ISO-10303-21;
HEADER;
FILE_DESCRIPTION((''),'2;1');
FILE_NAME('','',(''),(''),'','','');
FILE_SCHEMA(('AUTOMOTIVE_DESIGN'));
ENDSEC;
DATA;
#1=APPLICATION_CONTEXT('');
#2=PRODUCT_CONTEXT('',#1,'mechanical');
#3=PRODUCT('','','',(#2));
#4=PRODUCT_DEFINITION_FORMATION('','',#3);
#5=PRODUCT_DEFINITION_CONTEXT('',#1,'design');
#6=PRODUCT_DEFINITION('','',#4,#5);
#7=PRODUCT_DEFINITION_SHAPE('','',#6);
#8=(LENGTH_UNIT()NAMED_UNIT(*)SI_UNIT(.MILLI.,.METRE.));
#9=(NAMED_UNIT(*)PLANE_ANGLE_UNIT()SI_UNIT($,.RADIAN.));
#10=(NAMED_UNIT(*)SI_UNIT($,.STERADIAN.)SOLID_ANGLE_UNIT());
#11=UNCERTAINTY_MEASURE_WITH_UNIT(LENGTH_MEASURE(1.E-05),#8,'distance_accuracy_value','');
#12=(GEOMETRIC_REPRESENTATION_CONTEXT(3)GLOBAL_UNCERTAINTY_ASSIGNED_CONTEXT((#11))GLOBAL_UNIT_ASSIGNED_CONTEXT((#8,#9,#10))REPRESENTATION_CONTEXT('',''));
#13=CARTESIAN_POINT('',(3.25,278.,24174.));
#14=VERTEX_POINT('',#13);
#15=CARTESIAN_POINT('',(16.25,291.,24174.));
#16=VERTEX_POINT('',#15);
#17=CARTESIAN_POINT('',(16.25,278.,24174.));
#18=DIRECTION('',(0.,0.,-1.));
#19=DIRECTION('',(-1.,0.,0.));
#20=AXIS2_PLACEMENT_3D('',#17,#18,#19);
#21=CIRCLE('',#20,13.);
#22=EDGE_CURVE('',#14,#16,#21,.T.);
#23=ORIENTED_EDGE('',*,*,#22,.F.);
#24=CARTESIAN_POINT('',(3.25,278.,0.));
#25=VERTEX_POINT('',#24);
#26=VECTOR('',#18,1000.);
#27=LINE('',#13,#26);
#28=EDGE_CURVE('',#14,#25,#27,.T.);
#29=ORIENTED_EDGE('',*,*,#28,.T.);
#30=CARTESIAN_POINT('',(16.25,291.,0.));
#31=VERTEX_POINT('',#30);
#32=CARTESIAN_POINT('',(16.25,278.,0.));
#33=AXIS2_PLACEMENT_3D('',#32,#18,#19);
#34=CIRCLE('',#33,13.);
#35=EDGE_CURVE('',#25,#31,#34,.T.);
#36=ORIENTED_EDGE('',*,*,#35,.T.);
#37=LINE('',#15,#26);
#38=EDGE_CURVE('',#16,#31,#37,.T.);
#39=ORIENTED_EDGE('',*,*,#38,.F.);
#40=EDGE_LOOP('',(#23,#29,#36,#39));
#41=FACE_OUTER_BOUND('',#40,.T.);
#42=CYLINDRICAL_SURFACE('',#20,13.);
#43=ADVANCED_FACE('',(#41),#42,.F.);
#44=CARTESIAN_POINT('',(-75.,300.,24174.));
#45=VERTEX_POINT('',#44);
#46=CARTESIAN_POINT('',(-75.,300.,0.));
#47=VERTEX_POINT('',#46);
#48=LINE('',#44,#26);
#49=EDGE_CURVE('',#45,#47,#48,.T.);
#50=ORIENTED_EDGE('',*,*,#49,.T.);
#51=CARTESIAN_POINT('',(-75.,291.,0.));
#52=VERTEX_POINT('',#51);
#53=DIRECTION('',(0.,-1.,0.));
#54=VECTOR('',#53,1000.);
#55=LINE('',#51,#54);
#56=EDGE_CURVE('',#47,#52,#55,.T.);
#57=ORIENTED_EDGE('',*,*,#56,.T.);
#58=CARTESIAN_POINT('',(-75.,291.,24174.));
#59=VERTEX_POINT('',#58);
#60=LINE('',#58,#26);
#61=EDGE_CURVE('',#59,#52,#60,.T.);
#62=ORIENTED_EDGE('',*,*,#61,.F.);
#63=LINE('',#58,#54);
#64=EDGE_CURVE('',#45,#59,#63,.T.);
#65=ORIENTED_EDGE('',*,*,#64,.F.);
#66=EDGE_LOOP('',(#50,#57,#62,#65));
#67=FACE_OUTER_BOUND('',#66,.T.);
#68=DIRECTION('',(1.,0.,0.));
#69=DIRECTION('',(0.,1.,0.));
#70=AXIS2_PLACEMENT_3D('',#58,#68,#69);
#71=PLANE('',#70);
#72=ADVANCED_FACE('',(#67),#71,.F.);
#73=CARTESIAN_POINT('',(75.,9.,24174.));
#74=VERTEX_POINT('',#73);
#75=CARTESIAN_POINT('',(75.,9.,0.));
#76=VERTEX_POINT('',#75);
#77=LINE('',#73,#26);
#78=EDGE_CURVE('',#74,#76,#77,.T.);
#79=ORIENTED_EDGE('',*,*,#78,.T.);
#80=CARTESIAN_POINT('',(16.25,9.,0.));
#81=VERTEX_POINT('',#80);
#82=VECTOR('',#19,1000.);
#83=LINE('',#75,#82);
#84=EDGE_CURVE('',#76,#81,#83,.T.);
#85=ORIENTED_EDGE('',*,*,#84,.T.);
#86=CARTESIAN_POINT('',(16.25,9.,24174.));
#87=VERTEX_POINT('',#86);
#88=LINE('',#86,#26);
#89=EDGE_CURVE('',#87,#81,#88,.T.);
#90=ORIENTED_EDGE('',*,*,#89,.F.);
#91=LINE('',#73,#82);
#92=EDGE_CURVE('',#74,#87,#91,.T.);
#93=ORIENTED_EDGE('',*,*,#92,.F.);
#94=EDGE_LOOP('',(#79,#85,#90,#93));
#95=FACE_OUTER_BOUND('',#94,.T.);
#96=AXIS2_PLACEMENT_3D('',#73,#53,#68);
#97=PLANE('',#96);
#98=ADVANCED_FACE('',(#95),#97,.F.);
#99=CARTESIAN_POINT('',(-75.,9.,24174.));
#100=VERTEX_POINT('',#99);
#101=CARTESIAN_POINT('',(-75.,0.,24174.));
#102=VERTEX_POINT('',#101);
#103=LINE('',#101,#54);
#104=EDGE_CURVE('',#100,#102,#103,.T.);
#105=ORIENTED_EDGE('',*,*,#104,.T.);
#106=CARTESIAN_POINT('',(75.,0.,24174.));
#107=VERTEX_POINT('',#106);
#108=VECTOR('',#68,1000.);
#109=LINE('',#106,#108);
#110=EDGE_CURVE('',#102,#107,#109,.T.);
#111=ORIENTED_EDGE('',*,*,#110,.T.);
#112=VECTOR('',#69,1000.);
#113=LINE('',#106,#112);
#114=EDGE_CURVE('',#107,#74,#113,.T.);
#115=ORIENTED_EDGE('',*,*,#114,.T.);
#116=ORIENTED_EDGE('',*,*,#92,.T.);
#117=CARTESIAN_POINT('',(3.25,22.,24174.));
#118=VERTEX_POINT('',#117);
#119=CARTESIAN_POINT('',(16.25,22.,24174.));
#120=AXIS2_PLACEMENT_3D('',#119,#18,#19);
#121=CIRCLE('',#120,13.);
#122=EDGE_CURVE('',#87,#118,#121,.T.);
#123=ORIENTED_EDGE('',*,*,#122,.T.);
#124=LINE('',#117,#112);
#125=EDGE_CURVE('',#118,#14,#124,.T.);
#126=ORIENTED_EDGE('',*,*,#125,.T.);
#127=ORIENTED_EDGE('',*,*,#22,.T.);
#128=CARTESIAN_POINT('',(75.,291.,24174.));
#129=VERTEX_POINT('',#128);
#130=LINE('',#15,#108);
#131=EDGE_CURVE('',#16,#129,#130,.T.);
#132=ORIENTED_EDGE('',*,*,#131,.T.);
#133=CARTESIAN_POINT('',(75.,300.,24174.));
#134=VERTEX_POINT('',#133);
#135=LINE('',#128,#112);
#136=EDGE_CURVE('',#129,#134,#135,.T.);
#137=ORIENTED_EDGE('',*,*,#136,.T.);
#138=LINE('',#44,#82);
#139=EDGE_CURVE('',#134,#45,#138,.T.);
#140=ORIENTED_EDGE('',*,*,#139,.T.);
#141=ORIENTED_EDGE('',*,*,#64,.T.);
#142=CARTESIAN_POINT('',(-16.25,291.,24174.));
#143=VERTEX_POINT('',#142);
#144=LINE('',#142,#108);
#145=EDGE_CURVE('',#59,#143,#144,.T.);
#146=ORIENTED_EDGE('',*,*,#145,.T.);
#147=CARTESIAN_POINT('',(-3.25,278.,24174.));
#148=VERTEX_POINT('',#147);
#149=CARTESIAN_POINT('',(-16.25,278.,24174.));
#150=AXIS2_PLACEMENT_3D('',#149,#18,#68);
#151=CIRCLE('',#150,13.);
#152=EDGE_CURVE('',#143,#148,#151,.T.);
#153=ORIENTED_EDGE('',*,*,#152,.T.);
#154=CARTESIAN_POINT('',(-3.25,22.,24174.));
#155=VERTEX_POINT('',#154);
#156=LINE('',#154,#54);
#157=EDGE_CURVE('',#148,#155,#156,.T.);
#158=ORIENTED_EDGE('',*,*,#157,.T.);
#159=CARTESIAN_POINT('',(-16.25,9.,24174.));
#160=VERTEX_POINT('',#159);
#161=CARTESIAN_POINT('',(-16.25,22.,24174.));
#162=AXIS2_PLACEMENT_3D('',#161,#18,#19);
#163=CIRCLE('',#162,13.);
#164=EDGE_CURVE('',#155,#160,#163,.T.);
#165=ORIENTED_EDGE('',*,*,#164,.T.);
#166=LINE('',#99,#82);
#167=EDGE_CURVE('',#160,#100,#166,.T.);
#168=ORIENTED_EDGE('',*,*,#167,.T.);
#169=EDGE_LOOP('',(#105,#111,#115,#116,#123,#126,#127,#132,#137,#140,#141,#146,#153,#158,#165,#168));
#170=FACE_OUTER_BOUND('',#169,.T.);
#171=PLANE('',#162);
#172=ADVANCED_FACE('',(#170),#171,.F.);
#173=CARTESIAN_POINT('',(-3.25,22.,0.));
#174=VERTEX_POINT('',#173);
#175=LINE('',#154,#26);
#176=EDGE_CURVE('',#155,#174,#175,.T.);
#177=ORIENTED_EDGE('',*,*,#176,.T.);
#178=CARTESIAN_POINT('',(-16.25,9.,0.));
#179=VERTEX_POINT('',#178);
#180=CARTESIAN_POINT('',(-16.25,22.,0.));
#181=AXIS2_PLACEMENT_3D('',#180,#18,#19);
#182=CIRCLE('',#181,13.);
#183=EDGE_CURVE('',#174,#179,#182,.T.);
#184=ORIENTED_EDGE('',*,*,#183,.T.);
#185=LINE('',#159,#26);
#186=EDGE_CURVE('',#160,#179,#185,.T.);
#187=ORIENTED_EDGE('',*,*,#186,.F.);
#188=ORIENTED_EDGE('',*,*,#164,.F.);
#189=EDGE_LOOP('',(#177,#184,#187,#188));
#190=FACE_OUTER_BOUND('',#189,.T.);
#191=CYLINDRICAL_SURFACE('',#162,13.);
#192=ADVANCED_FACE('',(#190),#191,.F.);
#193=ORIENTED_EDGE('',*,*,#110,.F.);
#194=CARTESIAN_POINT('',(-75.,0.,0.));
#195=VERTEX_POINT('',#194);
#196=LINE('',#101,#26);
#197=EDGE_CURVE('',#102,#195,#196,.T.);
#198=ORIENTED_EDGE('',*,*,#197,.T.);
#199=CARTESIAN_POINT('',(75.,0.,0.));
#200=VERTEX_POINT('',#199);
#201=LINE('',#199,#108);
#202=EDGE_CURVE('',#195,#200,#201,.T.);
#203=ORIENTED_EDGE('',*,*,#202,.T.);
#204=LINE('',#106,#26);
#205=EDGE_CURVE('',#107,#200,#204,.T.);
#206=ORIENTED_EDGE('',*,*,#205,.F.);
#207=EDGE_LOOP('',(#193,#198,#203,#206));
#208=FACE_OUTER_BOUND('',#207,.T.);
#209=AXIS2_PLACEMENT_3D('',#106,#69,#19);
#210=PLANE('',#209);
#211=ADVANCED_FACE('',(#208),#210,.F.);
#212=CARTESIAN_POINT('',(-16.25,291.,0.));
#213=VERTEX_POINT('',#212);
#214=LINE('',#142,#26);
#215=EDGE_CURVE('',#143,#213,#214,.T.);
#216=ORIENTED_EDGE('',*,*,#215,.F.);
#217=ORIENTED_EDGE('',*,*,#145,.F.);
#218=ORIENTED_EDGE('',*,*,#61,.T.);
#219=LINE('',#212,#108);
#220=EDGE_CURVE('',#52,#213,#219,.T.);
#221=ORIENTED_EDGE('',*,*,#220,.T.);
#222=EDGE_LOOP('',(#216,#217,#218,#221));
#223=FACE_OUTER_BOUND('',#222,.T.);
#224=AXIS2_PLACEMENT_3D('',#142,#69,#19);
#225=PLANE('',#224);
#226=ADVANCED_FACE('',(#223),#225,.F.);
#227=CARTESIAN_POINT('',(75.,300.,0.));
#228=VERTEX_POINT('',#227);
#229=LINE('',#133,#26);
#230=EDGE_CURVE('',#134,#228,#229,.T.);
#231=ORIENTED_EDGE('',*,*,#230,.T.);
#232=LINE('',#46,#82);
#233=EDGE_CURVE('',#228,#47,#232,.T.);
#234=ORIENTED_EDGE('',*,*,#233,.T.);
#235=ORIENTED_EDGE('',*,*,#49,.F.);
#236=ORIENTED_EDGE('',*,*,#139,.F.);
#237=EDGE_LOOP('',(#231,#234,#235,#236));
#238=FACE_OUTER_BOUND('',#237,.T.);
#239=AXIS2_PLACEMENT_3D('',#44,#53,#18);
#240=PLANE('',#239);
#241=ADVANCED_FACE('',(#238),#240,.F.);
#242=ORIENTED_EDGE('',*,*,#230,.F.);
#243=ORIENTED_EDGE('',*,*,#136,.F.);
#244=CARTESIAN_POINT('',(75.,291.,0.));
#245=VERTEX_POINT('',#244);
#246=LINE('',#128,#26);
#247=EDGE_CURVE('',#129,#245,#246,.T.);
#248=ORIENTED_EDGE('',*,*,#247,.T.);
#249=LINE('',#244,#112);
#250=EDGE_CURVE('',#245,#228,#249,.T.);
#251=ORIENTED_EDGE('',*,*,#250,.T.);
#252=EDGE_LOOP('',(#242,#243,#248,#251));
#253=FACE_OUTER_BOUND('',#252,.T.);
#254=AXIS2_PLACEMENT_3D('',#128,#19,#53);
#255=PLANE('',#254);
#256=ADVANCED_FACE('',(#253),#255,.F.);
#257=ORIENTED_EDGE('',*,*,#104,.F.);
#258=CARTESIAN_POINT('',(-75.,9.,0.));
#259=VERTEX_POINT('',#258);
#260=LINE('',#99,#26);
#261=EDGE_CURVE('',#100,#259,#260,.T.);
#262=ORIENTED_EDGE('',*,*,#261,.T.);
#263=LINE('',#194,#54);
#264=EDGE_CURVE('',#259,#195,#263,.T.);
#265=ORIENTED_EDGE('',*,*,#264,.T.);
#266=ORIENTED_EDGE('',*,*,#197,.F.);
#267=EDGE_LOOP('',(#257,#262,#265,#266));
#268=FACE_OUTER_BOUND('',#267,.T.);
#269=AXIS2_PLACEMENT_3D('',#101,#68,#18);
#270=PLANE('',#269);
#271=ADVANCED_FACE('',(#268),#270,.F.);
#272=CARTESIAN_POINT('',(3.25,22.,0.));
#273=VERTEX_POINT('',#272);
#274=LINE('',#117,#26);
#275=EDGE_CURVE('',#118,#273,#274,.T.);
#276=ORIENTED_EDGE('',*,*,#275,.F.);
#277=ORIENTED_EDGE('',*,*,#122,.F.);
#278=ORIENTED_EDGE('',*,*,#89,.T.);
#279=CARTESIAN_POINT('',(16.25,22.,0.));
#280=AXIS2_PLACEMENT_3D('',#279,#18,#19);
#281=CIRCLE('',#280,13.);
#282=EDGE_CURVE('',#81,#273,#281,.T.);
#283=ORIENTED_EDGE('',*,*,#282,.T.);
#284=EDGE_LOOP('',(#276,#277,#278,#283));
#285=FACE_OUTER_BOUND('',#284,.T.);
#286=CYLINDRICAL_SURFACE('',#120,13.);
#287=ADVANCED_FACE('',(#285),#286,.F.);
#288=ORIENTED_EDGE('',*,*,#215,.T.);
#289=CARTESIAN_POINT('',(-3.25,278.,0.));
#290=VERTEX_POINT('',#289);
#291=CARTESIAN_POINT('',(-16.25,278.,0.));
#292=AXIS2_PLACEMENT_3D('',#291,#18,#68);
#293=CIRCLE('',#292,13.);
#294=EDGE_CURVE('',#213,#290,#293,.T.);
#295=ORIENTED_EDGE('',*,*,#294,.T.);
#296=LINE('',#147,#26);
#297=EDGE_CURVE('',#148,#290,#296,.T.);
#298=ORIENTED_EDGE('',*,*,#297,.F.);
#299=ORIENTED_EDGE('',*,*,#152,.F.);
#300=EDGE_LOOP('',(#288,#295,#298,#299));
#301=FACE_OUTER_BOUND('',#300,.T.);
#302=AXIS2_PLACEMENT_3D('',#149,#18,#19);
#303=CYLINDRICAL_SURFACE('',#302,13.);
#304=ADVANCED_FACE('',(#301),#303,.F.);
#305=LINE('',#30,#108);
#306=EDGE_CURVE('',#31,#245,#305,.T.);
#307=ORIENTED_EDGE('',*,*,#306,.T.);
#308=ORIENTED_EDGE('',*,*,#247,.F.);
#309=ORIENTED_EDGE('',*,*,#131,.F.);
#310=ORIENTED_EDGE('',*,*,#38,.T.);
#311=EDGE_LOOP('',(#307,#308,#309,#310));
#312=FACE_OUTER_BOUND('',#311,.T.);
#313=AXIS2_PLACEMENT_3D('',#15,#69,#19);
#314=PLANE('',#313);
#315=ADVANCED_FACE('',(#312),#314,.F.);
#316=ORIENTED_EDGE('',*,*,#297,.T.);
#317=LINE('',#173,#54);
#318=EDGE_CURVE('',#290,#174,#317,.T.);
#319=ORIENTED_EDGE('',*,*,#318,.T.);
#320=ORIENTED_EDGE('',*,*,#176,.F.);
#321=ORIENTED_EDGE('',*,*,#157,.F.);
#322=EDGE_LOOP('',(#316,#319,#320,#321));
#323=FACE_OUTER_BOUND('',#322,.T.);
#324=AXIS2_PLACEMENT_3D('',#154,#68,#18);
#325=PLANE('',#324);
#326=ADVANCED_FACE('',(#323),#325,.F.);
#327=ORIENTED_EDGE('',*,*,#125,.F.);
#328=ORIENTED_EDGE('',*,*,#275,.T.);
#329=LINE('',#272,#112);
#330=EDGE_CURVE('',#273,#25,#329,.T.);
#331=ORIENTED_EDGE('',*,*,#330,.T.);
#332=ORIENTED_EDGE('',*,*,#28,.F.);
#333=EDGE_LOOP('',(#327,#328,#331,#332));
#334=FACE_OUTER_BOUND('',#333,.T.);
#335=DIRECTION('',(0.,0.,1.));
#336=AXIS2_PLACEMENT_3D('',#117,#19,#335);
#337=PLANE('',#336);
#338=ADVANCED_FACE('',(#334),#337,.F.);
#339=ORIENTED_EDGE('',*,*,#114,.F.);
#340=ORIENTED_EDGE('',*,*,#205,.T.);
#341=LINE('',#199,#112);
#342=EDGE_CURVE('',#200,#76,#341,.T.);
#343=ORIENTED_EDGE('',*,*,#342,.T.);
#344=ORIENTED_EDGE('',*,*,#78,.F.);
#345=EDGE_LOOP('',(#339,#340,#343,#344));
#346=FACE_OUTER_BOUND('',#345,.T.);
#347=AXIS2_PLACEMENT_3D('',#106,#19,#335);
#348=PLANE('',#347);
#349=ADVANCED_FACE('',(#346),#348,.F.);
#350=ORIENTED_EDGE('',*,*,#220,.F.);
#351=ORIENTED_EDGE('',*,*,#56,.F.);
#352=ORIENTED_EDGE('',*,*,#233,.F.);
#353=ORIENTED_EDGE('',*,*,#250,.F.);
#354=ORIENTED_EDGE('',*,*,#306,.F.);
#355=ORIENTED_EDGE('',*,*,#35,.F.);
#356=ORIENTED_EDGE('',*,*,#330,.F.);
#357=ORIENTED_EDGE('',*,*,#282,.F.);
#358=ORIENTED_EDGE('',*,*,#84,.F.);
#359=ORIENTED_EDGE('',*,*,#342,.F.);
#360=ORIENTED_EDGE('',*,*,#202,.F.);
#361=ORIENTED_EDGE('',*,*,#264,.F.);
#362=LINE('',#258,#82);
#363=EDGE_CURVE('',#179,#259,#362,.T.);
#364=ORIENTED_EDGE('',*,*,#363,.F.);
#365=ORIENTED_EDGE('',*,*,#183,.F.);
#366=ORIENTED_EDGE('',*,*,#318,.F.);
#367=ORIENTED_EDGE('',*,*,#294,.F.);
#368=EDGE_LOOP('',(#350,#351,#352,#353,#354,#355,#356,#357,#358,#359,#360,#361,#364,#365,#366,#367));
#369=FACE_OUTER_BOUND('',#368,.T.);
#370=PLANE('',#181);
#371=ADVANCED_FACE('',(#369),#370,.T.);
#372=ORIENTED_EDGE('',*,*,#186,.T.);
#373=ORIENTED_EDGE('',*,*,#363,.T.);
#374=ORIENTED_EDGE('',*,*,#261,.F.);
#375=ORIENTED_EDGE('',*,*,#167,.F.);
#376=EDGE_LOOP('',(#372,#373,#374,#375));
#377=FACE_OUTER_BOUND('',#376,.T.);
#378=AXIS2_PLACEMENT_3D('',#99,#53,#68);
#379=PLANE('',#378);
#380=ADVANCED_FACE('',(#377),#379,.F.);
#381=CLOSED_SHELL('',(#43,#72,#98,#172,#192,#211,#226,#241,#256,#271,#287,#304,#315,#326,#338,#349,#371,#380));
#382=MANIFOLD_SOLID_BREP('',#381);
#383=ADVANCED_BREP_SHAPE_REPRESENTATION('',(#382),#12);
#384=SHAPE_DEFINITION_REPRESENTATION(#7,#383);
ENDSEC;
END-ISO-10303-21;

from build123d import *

# Parameters (mm, degrees)
BOSS_EXTRUDE1_DEPTH = 24174


with BuildPart() as part:
    # Sketch1 → Boss-Extrude1 (new body)
    with BuildSketch(Plane.XY):
        with BuildLine():
            Line((75, 0), (-75, 0))
            Line((-75, 0), (-75, 9))
            Line((-75, 9), (-16.25, 9))
            ThreePointArc((-16.25, 9), (-7.057611845, 12.807611845), (-3.25, 22))
            Line((-3.25, 22), (-3.25, 278))
            ThreePointArc((-3.25, 278), (-7.057611845, 287.192388155), (-16.25, 291))
            Line((-16.25, 291), (-75, 291))
            Line((-75, 291), (-75, 300))
            Line((-75, 300), (75, 300))
            Line((75, 300), (75, 291))
            Line((75, 291), (16.25, 291))
            ThreePointArc((16.25, 291), (7.057611845, 287.192388155), (3.25, 278))
            Line((3.25, 278), (3.25, 22))
            ThreePointArc((3.25, 22), (7.057611845, 12.807611845), (16.25, 9))
            Line((16.25, 9), (75, 9))
            Line((75, 9), (75, 0))
        make_face()
    extrude(amount=BOSS_EXTRUDE1_DEPTH)


solid = part.part
